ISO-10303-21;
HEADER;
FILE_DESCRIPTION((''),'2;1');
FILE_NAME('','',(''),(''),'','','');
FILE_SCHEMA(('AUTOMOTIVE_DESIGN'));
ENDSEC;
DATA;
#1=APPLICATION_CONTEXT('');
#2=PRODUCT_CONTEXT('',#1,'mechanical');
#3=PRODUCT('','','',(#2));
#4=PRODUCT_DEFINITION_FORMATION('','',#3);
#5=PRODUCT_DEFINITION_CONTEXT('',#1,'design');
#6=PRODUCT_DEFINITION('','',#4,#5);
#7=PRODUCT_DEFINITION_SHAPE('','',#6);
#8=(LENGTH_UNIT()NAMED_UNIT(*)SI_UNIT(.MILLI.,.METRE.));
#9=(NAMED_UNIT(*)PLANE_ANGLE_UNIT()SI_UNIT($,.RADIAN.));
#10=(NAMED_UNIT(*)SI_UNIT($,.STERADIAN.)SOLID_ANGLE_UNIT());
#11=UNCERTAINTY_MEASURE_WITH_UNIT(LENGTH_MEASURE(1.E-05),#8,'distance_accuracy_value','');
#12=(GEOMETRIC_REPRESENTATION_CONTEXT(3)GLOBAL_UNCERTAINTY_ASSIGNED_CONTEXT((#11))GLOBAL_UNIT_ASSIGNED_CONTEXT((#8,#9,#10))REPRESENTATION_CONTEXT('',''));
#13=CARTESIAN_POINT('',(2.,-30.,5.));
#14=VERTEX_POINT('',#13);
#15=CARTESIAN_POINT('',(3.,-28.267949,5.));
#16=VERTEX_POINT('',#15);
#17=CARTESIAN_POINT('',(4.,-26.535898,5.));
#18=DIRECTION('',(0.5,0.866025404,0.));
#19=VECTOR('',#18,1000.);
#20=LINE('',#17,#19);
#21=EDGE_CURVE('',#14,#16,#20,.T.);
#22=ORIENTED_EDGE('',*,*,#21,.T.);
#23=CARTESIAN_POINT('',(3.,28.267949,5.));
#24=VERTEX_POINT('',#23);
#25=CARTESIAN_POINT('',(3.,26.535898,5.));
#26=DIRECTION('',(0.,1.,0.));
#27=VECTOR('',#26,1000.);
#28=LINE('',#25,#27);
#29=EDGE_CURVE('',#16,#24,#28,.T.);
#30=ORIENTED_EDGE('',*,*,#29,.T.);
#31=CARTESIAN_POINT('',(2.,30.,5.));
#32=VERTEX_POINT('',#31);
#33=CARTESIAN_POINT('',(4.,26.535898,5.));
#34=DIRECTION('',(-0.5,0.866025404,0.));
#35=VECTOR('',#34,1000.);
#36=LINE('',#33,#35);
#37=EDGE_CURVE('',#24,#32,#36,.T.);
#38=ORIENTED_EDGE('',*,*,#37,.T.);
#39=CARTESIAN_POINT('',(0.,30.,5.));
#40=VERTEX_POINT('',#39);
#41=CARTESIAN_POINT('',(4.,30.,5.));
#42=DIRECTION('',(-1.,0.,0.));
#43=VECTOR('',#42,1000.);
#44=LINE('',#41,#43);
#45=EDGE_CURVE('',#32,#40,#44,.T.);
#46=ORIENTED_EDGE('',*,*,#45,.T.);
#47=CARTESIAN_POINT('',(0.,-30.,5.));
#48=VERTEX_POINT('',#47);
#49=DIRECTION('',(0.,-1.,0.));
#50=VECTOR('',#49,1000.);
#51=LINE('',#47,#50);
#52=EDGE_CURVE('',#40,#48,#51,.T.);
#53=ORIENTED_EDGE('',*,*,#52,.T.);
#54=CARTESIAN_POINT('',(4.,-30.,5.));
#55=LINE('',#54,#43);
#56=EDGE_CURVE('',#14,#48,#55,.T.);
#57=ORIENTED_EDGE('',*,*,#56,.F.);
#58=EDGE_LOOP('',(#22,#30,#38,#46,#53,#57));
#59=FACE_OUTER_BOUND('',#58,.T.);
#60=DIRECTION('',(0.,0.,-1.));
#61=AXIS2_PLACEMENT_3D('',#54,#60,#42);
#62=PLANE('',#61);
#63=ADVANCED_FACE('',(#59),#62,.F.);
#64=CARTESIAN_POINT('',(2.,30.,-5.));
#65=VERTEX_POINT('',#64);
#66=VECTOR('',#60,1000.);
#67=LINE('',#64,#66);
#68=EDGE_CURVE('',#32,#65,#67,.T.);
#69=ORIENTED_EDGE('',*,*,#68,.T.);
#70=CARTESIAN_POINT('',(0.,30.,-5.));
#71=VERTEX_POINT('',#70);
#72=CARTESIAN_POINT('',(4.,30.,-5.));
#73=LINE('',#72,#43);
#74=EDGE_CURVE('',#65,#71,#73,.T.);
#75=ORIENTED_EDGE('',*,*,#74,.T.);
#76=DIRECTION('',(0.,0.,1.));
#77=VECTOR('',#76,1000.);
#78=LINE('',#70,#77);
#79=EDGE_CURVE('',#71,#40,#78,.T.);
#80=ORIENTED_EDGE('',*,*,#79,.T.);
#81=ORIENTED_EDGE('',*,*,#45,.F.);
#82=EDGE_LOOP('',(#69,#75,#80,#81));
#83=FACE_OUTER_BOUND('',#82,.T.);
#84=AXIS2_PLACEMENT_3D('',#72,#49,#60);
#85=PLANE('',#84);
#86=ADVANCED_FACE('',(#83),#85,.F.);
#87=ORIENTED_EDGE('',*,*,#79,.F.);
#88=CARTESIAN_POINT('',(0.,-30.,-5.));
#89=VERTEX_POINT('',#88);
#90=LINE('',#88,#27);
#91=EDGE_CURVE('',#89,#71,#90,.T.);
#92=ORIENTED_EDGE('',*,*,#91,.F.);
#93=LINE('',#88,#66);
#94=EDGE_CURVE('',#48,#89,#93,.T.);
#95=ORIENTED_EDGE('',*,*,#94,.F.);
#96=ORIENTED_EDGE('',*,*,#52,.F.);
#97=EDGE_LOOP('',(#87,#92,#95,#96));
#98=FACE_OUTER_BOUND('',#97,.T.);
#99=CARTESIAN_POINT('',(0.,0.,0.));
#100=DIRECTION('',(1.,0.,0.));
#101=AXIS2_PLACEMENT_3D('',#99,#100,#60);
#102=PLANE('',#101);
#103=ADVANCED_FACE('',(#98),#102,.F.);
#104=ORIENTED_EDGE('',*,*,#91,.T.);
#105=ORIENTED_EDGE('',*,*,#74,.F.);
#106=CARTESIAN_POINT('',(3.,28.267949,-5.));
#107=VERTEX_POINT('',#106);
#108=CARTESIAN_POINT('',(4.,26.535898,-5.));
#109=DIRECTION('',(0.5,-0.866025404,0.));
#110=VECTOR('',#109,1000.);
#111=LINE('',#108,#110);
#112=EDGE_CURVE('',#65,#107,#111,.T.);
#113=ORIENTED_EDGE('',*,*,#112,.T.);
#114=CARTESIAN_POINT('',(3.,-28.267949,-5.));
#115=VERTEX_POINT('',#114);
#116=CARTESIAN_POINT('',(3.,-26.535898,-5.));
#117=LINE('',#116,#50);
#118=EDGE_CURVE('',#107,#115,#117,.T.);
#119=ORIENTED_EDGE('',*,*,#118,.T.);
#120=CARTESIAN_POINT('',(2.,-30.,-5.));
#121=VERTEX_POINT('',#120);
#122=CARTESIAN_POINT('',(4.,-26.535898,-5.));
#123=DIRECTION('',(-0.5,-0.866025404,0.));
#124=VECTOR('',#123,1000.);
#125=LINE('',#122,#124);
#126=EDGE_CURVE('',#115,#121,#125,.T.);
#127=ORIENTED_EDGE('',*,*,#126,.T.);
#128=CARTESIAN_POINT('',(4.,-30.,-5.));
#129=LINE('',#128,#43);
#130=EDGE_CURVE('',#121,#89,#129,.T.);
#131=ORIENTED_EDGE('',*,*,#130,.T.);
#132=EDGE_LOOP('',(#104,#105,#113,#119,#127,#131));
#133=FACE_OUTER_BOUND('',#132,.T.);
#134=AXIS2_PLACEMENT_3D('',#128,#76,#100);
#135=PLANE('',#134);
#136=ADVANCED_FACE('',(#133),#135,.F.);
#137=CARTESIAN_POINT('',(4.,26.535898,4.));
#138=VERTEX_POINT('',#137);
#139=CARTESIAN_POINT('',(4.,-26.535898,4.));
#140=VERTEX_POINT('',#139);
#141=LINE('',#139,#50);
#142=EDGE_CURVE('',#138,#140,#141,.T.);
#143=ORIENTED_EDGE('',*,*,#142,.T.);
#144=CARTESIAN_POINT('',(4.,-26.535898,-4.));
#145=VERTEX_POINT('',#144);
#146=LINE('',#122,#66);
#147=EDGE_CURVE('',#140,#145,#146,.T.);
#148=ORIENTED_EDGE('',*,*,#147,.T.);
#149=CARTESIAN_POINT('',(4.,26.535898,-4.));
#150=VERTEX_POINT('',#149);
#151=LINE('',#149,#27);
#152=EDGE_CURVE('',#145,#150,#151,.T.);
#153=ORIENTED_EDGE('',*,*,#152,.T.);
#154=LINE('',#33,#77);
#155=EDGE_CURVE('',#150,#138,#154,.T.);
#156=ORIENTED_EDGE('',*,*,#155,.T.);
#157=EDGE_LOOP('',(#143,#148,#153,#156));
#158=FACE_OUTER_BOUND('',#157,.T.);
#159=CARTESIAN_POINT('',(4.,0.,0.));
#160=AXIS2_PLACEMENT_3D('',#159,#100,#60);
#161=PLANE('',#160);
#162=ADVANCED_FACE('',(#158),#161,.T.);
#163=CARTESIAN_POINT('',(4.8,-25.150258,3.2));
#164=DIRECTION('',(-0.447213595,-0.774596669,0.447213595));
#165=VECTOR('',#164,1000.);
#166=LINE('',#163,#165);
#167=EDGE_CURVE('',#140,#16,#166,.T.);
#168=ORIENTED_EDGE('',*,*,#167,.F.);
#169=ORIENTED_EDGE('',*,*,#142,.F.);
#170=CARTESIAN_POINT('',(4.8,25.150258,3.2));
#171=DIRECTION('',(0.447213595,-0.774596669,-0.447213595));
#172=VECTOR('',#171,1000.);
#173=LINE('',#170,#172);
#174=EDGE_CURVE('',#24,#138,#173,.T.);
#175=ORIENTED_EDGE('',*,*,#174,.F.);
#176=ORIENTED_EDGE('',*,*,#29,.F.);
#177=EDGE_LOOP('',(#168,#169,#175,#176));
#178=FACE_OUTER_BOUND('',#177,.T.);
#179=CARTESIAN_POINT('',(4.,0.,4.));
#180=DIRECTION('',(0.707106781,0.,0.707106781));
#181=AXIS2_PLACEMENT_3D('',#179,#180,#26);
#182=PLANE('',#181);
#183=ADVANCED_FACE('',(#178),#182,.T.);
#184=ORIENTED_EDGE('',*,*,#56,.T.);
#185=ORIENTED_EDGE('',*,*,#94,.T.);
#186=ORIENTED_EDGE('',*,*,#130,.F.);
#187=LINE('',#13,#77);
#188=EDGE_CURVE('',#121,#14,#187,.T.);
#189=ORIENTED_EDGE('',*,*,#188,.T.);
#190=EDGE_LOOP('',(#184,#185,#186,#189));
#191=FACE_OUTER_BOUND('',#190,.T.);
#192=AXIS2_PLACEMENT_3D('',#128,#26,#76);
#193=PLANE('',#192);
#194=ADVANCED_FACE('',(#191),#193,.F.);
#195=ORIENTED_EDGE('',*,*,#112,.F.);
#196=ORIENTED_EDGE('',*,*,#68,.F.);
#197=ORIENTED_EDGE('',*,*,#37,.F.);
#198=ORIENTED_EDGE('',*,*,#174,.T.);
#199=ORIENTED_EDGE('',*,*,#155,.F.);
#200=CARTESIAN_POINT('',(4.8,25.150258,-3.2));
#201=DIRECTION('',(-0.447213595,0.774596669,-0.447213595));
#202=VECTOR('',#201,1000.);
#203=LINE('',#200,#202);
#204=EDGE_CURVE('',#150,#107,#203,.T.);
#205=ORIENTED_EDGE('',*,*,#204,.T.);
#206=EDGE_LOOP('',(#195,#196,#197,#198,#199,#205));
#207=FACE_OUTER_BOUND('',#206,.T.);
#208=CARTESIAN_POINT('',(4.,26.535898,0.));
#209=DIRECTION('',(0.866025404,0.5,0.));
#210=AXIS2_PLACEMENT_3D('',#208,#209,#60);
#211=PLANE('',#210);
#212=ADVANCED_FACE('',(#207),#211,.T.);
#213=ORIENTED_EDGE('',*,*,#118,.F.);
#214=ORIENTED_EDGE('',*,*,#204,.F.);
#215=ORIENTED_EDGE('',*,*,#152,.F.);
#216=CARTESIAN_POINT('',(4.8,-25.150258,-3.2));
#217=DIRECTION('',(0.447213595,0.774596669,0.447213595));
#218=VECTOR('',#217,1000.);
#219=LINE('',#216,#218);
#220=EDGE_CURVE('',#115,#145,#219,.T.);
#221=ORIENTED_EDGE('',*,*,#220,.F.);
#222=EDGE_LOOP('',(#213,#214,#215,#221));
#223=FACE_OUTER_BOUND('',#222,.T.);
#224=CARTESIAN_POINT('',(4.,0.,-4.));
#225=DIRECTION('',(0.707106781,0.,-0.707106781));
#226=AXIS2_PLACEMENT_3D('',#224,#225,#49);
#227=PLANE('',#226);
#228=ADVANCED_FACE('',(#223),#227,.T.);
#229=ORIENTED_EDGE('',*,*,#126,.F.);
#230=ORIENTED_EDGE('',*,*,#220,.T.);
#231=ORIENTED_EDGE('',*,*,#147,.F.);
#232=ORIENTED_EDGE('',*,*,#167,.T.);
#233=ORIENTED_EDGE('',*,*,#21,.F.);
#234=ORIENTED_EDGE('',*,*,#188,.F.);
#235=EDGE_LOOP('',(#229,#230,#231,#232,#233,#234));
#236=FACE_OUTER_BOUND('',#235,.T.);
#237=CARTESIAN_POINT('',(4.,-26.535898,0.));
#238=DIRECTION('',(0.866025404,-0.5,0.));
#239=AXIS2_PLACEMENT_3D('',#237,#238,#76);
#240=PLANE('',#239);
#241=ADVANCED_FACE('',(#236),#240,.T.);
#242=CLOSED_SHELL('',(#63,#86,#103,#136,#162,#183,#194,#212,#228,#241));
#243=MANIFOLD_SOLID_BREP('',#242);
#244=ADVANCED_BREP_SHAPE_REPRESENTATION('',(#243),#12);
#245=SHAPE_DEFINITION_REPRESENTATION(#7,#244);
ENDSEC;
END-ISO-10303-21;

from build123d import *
from OCP.BRepFilletAPI import BRepFilletAPI_MakeChamfer

# Parameters (mm, degrees)
SKETCH_1_W      = 10
SKETCH_1_H      = 60
EXTRUDE_1_DEPTH = 4
CHAMFER_1_SIZE  = 2
CHAMFER_1_SIZE2 = 3.464101615
CHAMFER_2_SIZE  = 1


with BuildPart() as part:
    # 草图1 → 凸台-拉伸1 (new body)
    with BuildSketch(Plane(origin=(0, 0, 0), x_dir=(0, 0, -1), z_dir=(1, 0, 0))):
        Rectangle(SKETCH_1_W, SKETCH_1_H)
    extrude(amount=EXTRUDE_1_DEPTH)

    # 倒角1: one chamfer whose edges measure the first distance from different faces: ONE call of the kernel's chamfer builder (chamfer() names one face for all edges)
    chamfer_1_edges_1 = [part.edges().sort_by_distance(p)[0] for p in [
        (4, 30, 0),
    ]]
    chamfer_1_side_1 = [part.faces().sort_by_distance(p)[0] for p in [
        (2, 30, 0),
    ]]
    chamfer_1_edges_2 = [part.edges().sort_by_distance(p)[0] for p in [
        (4, -30, 0),
    ]]
    chamfer_1_side_2 = [part.faces().sort_by_distance(p)[0] for p in [
        (2, -30, 0),
    ]]
    chamfer_1 = BRepFilletAPI_MakeChamfer(part.part.solid().wrapped)
    for e in chamfer_1_edges_1:
        chamfer_1.Add(CHAMFER_1_SIZE, CHAMFER_1_SIZE2, e.wrapped, chamfer_1_side_1[0].wrapped)  # the first distance lies on this face
    for e in chamfer_1_edges_2:
        chamfer_1.Add(CHAMFER_1_SIZE, CHAMFER_1_SIZE2, e.wrapped, chamfer_1_side_2[0].wrapped)  # the first distance lies on this face
    add(Compound.cast(chamfer_1.Shape()), mode=Mode.REPLACE)

    # 倒角2
    chamfer_2_edges = [part.edges().sort_by_distance(p)[0] for p in [
        (4, 0, 5),
        (4, 0, -5),
    ]]
    chamfer(chamfer_2_edges, length=CHAMFER_2_SIZE)


solid = part.part
